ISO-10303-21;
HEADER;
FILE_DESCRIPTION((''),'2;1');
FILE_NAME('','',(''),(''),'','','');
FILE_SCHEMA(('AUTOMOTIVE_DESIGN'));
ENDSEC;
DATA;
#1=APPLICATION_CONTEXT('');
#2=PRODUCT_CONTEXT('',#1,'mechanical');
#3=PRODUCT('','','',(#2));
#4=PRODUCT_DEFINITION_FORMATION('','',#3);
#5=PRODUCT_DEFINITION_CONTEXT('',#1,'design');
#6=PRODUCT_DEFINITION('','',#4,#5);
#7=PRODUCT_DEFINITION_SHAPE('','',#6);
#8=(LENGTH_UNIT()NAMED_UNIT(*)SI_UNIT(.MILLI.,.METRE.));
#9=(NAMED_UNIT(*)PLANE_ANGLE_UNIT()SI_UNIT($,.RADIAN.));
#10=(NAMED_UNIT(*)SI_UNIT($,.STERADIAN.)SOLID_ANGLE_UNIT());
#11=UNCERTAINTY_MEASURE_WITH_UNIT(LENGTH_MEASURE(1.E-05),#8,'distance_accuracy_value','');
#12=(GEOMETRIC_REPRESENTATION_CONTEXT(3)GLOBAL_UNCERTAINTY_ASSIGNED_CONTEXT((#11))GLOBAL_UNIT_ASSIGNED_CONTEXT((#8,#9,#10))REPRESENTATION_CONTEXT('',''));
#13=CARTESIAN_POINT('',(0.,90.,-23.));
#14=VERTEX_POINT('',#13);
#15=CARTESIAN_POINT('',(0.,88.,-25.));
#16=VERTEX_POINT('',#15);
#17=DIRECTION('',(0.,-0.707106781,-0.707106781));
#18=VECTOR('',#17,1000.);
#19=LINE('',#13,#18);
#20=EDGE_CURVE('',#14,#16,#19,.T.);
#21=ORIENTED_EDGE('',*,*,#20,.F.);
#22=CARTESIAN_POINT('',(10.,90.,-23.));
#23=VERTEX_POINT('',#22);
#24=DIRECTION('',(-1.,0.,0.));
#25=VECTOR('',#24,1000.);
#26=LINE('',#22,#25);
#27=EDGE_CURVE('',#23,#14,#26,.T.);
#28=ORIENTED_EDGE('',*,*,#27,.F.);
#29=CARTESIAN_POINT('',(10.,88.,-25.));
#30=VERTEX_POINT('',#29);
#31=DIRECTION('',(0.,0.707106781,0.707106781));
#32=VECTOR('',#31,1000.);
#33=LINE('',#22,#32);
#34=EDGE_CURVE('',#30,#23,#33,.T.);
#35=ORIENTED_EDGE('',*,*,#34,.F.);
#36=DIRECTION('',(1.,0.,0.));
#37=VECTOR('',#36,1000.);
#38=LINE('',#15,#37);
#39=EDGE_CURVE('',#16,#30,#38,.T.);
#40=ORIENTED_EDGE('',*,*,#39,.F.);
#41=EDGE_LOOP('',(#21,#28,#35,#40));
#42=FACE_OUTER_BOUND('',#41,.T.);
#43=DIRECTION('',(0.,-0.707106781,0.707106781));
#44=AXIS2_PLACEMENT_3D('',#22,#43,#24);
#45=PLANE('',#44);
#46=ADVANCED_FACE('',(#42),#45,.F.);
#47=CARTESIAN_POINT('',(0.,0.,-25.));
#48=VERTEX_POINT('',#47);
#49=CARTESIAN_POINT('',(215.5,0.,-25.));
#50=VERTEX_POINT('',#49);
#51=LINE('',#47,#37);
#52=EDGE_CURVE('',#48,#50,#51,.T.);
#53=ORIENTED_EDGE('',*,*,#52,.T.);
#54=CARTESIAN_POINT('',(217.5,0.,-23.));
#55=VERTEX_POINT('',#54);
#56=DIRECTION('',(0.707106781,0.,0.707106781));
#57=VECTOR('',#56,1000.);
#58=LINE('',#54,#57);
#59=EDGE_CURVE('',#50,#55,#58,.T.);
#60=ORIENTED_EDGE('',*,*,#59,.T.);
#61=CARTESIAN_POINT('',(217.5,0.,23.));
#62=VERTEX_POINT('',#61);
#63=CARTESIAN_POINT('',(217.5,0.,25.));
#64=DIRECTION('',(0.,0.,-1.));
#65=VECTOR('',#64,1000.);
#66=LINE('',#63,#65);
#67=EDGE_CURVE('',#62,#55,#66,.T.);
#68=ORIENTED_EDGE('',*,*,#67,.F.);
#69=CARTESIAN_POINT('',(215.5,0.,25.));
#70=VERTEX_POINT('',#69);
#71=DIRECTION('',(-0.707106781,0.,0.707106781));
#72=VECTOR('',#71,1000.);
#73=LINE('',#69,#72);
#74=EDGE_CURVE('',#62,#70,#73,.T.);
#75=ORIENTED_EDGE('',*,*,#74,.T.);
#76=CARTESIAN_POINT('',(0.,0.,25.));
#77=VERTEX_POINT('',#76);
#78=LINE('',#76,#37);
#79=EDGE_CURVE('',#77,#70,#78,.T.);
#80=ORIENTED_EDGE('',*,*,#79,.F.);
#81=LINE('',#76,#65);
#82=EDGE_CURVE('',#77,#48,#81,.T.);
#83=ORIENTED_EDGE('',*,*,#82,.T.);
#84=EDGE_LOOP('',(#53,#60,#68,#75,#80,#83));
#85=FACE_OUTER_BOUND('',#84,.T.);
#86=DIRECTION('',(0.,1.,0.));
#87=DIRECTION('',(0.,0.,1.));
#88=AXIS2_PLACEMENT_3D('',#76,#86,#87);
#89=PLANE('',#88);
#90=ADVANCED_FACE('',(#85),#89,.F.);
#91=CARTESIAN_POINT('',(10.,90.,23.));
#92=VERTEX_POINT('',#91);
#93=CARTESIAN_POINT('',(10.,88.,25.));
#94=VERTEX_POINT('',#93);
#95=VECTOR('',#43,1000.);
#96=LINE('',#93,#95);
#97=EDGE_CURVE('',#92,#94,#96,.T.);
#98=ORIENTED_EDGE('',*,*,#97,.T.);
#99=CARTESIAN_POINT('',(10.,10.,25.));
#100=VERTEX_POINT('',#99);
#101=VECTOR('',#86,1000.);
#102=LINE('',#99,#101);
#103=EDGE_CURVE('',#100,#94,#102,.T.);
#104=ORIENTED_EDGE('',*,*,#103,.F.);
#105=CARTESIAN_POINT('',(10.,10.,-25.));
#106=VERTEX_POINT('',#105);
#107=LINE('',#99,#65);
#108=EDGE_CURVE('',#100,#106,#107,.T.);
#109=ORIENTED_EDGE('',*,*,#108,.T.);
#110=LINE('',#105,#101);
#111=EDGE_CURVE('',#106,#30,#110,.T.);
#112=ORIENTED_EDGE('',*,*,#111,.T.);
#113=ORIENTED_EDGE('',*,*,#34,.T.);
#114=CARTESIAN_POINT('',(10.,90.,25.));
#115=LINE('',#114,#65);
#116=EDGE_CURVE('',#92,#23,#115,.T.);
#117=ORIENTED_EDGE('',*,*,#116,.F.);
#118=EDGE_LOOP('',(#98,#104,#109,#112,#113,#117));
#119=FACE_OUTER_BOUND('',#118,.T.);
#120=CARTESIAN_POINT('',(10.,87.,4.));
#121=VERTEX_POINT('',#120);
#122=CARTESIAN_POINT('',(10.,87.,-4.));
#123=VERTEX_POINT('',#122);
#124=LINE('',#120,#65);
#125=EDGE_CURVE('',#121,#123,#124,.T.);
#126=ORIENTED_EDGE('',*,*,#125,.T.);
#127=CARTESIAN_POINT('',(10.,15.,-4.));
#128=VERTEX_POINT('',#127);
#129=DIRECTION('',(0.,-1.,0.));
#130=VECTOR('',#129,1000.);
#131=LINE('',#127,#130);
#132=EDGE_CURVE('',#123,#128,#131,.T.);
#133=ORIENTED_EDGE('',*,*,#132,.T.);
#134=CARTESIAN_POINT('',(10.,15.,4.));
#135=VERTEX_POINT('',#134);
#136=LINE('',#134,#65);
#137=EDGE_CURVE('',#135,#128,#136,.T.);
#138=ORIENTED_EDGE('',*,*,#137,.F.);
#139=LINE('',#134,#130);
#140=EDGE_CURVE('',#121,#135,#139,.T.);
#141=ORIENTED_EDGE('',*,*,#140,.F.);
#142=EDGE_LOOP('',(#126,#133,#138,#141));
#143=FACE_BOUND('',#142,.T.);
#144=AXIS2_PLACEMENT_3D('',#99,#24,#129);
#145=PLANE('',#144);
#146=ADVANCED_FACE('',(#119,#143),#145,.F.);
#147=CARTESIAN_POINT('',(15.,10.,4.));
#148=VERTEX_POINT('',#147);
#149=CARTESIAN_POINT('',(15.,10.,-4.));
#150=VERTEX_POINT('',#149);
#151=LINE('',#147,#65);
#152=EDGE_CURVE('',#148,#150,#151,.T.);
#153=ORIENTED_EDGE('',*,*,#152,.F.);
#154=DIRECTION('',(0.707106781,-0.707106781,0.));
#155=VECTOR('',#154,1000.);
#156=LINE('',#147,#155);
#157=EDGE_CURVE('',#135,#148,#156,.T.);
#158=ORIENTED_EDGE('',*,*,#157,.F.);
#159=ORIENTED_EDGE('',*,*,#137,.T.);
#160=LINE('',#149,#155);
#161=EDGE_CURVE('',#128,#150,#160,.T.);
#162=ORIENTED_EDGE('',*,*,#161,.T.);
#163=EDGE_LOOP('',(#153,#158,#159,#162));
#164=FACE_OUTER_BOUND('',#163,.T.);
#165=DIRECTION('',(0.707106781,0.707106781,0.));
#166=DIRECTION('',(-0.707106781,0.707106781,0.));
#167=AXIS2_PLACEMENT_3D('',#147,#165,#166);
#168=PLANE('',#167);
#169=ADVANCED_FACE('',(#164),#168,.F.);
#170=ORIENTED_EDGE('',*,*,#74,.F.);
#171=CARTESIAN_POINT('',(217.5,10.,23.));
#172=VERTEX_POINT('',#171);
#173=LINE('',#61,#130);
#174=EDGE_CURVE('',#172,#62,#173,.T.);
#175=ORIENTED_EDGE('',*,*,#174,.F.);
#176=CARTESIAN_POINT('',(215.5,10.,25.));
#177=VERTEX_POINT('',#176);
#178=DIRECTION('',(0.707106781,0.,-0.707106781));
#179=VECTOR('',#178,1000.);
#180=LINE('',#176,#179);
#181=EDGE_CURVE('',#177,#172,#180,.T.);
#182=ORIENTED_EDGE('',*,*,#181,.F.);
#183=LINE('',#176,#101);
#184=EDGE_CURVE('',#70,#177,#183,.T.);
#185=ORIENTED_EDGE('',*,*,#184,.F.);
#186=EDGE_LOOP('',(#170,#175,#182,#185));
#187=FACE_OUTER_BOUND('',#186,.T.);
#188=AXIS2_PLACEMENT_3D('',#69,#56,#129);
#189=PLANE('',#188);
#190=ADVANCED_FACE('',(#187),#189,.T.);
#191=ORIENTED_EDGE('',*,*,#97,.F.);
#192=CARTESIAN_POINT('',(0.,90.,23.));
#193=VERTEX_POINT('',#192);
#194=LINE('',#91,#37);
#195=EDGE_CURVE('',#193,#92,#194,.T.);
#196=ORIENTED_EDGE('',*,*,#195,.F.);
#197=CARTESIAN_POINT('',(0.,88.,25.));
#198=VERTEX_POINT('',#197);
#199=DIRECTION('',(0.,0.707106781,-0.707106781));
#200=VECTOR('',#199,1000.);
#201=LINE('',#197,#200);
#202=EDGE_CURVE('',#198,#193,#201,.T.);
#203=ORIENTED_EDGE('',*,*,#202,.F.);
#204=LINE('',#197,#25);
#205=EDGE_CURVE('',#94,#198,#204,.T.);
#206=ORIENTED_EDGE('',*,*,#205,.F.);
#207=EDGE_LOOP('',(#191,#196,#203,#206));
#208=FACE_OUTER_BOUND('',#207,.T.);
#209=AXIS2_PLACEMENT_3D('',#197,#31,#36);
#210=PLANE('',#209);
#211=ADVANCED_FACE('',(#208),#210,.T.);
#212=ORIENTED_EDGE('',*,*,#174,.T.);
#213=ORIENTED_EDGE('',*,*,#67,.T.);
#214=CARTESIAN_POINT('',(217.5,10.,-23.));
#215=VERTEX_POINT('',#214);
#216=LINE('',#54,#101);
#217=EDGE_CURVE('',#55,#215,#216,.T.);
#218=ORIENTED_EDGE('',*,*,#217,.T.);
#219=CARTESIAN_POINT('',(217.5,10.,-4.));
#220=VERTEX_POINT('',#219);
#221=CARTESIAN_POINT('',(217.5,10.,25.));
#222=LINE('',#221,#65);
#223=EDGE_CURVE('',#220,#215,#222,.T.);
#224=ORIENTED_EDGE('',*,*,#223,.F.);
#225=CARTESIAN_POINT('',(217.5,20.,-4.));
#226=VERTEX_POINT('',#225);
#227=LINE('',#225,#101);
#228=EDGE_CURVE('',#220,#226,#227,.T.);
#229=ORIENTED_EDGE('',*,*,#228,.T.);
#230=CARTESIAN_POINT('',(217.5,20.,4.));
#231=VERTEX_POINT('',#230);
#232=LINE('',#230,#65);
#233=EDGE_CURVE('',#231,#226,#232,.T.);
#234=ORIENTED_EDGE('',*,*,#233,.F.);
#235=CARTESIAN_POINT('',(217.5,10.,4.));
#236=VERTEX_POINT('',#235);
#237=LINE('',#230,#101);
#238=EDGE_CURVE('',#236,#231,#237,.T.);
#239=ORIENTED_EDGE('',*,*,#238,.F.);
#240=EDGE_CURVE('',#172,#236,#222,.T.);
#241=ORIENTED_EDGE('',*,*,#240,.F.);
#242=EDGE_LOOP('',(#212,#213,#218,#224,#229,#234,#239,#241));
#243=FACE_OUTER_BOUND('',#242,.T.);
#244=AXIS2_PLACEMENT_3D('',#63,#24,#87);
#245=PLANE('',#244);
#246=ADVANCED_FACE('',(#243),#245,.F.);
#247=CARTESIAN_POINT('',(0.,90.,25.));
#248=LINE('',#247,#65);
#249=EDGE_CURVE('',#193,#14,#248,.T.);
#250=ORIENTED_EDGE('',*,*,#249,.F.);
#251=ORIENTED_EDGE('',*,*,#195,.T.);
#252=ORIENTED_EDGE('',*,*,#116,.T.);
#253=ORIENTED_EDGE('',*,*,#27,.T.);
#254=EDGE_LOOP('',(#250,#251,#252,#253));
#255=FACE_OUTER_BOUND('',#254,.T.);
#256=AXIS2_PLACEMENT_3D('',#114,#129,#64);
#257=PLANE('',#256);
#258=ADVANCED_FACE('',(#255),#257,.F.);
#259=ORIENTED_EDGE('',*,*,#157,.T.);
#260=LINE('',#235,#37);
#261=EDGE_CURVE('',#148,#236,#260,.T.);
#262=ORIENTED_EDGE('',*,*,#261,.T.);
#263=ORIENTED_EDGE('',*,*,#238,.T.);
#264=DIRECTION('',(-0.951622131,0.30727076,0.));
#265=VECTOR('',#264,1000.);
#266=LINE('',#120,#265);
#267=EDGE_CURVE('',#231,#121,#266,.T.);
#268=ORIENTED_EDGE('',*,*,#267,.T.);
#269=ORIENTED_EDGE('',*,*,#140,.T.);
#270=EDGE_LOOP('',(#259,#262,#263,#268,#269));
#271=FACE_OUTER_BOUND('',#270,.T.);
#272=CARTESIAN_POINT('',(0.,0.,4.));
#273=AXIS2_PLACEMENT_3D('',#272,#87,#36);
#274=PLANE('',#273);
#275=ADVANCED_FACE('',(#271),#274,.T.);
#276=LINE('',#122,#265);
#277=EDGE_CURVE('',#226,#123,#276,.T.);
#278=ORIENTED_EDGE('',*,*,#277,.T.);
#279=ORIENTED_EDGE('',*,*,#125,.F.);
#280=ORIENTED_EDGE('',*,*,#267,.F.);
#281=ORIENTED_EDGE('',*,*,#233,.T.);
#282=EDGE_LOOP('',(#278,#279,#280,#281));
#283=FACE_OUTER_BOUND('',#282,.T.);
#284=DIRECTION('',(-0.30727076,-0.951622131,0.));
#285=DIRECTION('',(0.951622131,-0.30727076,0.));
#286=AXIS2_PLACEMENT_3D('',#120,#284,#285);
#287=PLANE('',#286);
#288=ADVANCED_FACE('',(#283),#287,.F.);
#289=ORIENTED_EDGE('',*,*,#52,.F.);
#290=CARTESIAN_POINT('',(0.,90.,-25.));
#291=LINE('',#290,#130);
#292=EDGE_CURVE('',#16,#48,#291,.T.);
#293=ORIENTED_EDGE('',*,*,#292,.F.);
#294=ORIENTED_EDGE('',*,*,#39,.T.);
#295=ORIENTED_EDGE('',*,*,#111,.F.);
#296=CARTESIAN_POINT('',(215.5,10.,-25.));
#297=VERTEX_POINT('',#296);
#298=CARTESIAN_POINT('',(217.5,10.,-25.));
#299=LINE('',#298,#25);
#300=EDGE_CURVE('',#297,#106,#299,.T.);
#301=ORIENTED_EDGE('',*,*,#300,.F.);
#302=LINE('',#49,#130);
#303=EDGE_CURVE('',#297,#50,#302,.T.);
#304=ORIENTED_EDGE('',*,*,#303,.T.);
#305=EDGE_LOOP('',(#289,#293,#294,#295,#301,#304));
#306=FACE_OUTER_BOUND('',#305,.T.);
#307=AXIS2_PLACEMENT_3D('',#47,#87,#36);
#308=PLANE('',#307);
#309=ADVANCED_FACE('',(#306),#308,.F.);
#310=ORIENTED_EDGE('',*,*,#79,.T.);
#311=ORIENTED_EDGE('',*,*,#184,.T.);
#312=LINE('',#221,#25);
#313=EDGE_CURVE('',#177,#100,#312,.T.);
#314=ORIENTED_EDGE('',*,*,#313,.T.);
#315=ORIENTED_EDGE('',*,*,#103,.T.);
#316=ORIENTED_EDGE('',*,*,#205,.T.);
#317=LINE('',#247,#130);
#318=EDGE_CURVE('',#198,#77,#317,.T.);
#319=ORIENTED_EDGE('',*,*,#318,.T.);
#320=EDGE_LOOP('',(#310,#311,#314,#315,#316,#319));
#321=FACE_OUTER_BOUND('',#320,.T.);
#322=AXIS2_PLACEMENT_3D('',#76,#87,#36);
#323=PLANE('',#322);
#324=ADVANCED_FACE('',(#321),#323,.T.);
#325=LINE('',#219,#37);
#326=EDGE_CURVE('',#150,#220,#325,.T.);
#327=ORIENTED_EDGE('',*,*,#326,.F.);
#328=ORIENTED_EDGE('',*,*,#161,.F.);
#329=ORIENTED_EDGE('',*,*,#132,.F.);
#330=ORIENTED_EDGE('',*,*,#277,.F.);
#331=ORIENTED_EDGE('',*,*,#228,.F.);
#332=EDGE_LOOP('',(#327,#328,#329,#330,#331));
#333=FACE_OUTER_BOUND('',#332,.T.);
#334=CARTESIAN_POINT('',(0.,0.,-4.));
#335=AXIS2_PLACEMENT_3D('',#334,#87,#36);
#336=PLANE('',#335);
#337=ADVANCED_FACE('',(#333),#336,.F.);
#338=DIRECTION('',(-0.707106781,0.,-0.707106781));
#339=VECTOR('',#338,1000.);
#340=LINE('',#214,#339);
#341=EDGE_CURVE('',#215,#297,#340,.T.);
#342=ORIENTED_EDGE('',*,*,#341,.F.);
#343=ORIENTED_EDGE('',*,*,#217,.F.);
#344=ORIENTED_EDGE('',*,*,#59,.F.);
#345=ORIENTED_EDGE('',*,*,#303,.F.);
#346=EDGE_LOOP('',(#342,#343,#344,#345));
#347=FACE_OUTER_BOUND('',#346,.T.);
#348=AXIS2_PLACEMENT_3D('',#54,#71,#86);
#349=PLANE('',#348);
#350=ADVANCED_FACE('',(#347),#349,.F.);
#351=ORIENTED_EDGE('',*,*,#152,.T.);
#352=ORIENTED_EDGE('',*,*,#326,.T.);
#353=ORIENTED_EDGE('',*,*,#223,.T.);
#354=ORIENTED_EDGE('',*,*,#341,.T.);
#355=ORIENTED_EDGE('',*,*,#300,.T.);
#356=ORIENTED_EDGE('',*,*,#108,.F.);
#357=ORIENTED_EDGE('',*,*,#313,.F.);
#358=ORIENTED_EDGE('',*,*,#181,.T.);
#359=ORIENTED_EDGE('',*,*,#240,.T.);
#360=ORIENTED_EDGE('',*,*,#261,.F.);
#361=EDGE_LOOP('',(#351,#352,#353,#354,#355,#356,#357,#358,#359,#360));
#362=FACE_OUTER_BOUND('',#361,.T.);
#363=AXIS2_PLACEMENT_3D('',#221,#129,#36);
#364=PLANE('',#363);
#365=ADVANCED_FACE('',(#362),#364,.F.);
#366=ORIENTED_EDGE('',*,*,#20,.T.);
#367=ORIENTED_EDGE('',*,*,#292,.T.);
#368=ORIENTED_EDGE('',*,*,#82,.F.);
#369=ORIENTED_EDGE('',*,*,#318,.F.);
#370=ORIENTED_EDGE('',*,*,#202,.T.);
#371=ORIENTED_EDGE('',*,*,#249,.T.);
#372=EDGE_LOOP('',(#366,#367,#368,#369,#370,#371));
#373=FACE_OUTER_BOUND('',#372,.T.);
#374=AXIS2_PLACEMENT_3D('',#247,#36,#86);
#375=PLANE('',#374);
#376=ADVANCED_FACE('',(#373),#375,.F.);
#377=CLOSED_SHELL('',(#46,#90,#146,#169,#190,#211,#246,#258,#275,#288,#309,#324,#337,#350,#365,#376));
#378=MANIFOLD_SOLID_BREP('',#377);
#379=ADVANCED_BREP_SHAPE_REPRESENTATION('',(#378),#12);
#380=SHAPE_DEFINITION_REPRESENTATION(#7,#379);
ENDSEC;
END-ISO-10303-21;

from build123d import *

# Parameters (mm, degrees)
EXTRUDE_1_DEPTH = 25
EXTRUDE_2_DEPTH = 4
CHAMFER_1_SIZE  = 2


with BuildPart() as part:
    # 草图1 → 凸台-拉伸1 (new, symmetric)
    with BuildSketch(Plane.XY):
        Polygon((0, 0), (217.5, 0), (217.5, 10), (10, 10), (10, 90), (0, 90), align=None)
    extrude(amount=EXTRUDE_1_DEPTH, both=True)

    # 草图2 → 凸台-拉伸2 (add, symmetric)
    with BuildSketch(Plane.XY):
        Polygon((10, 87), (217.5, 20), (217.5, 10), (15, 10), (10, 15), align=None)
    extrude(amount=EXTRUDE_2_DEPTH, both=True)

    # 倒角1
    chamfer_1_edges = [part.edges().sort_by_distance(p)[0] for p in [
        (217.5, 5, 25),
        (5, 90, 25),
        (5, 90, -25),
        (217.5, 5, -25),
    ]]
    chamfer(chamfer_1_edges, length=CHAMFER_1_SIZE)


solid = part.part
